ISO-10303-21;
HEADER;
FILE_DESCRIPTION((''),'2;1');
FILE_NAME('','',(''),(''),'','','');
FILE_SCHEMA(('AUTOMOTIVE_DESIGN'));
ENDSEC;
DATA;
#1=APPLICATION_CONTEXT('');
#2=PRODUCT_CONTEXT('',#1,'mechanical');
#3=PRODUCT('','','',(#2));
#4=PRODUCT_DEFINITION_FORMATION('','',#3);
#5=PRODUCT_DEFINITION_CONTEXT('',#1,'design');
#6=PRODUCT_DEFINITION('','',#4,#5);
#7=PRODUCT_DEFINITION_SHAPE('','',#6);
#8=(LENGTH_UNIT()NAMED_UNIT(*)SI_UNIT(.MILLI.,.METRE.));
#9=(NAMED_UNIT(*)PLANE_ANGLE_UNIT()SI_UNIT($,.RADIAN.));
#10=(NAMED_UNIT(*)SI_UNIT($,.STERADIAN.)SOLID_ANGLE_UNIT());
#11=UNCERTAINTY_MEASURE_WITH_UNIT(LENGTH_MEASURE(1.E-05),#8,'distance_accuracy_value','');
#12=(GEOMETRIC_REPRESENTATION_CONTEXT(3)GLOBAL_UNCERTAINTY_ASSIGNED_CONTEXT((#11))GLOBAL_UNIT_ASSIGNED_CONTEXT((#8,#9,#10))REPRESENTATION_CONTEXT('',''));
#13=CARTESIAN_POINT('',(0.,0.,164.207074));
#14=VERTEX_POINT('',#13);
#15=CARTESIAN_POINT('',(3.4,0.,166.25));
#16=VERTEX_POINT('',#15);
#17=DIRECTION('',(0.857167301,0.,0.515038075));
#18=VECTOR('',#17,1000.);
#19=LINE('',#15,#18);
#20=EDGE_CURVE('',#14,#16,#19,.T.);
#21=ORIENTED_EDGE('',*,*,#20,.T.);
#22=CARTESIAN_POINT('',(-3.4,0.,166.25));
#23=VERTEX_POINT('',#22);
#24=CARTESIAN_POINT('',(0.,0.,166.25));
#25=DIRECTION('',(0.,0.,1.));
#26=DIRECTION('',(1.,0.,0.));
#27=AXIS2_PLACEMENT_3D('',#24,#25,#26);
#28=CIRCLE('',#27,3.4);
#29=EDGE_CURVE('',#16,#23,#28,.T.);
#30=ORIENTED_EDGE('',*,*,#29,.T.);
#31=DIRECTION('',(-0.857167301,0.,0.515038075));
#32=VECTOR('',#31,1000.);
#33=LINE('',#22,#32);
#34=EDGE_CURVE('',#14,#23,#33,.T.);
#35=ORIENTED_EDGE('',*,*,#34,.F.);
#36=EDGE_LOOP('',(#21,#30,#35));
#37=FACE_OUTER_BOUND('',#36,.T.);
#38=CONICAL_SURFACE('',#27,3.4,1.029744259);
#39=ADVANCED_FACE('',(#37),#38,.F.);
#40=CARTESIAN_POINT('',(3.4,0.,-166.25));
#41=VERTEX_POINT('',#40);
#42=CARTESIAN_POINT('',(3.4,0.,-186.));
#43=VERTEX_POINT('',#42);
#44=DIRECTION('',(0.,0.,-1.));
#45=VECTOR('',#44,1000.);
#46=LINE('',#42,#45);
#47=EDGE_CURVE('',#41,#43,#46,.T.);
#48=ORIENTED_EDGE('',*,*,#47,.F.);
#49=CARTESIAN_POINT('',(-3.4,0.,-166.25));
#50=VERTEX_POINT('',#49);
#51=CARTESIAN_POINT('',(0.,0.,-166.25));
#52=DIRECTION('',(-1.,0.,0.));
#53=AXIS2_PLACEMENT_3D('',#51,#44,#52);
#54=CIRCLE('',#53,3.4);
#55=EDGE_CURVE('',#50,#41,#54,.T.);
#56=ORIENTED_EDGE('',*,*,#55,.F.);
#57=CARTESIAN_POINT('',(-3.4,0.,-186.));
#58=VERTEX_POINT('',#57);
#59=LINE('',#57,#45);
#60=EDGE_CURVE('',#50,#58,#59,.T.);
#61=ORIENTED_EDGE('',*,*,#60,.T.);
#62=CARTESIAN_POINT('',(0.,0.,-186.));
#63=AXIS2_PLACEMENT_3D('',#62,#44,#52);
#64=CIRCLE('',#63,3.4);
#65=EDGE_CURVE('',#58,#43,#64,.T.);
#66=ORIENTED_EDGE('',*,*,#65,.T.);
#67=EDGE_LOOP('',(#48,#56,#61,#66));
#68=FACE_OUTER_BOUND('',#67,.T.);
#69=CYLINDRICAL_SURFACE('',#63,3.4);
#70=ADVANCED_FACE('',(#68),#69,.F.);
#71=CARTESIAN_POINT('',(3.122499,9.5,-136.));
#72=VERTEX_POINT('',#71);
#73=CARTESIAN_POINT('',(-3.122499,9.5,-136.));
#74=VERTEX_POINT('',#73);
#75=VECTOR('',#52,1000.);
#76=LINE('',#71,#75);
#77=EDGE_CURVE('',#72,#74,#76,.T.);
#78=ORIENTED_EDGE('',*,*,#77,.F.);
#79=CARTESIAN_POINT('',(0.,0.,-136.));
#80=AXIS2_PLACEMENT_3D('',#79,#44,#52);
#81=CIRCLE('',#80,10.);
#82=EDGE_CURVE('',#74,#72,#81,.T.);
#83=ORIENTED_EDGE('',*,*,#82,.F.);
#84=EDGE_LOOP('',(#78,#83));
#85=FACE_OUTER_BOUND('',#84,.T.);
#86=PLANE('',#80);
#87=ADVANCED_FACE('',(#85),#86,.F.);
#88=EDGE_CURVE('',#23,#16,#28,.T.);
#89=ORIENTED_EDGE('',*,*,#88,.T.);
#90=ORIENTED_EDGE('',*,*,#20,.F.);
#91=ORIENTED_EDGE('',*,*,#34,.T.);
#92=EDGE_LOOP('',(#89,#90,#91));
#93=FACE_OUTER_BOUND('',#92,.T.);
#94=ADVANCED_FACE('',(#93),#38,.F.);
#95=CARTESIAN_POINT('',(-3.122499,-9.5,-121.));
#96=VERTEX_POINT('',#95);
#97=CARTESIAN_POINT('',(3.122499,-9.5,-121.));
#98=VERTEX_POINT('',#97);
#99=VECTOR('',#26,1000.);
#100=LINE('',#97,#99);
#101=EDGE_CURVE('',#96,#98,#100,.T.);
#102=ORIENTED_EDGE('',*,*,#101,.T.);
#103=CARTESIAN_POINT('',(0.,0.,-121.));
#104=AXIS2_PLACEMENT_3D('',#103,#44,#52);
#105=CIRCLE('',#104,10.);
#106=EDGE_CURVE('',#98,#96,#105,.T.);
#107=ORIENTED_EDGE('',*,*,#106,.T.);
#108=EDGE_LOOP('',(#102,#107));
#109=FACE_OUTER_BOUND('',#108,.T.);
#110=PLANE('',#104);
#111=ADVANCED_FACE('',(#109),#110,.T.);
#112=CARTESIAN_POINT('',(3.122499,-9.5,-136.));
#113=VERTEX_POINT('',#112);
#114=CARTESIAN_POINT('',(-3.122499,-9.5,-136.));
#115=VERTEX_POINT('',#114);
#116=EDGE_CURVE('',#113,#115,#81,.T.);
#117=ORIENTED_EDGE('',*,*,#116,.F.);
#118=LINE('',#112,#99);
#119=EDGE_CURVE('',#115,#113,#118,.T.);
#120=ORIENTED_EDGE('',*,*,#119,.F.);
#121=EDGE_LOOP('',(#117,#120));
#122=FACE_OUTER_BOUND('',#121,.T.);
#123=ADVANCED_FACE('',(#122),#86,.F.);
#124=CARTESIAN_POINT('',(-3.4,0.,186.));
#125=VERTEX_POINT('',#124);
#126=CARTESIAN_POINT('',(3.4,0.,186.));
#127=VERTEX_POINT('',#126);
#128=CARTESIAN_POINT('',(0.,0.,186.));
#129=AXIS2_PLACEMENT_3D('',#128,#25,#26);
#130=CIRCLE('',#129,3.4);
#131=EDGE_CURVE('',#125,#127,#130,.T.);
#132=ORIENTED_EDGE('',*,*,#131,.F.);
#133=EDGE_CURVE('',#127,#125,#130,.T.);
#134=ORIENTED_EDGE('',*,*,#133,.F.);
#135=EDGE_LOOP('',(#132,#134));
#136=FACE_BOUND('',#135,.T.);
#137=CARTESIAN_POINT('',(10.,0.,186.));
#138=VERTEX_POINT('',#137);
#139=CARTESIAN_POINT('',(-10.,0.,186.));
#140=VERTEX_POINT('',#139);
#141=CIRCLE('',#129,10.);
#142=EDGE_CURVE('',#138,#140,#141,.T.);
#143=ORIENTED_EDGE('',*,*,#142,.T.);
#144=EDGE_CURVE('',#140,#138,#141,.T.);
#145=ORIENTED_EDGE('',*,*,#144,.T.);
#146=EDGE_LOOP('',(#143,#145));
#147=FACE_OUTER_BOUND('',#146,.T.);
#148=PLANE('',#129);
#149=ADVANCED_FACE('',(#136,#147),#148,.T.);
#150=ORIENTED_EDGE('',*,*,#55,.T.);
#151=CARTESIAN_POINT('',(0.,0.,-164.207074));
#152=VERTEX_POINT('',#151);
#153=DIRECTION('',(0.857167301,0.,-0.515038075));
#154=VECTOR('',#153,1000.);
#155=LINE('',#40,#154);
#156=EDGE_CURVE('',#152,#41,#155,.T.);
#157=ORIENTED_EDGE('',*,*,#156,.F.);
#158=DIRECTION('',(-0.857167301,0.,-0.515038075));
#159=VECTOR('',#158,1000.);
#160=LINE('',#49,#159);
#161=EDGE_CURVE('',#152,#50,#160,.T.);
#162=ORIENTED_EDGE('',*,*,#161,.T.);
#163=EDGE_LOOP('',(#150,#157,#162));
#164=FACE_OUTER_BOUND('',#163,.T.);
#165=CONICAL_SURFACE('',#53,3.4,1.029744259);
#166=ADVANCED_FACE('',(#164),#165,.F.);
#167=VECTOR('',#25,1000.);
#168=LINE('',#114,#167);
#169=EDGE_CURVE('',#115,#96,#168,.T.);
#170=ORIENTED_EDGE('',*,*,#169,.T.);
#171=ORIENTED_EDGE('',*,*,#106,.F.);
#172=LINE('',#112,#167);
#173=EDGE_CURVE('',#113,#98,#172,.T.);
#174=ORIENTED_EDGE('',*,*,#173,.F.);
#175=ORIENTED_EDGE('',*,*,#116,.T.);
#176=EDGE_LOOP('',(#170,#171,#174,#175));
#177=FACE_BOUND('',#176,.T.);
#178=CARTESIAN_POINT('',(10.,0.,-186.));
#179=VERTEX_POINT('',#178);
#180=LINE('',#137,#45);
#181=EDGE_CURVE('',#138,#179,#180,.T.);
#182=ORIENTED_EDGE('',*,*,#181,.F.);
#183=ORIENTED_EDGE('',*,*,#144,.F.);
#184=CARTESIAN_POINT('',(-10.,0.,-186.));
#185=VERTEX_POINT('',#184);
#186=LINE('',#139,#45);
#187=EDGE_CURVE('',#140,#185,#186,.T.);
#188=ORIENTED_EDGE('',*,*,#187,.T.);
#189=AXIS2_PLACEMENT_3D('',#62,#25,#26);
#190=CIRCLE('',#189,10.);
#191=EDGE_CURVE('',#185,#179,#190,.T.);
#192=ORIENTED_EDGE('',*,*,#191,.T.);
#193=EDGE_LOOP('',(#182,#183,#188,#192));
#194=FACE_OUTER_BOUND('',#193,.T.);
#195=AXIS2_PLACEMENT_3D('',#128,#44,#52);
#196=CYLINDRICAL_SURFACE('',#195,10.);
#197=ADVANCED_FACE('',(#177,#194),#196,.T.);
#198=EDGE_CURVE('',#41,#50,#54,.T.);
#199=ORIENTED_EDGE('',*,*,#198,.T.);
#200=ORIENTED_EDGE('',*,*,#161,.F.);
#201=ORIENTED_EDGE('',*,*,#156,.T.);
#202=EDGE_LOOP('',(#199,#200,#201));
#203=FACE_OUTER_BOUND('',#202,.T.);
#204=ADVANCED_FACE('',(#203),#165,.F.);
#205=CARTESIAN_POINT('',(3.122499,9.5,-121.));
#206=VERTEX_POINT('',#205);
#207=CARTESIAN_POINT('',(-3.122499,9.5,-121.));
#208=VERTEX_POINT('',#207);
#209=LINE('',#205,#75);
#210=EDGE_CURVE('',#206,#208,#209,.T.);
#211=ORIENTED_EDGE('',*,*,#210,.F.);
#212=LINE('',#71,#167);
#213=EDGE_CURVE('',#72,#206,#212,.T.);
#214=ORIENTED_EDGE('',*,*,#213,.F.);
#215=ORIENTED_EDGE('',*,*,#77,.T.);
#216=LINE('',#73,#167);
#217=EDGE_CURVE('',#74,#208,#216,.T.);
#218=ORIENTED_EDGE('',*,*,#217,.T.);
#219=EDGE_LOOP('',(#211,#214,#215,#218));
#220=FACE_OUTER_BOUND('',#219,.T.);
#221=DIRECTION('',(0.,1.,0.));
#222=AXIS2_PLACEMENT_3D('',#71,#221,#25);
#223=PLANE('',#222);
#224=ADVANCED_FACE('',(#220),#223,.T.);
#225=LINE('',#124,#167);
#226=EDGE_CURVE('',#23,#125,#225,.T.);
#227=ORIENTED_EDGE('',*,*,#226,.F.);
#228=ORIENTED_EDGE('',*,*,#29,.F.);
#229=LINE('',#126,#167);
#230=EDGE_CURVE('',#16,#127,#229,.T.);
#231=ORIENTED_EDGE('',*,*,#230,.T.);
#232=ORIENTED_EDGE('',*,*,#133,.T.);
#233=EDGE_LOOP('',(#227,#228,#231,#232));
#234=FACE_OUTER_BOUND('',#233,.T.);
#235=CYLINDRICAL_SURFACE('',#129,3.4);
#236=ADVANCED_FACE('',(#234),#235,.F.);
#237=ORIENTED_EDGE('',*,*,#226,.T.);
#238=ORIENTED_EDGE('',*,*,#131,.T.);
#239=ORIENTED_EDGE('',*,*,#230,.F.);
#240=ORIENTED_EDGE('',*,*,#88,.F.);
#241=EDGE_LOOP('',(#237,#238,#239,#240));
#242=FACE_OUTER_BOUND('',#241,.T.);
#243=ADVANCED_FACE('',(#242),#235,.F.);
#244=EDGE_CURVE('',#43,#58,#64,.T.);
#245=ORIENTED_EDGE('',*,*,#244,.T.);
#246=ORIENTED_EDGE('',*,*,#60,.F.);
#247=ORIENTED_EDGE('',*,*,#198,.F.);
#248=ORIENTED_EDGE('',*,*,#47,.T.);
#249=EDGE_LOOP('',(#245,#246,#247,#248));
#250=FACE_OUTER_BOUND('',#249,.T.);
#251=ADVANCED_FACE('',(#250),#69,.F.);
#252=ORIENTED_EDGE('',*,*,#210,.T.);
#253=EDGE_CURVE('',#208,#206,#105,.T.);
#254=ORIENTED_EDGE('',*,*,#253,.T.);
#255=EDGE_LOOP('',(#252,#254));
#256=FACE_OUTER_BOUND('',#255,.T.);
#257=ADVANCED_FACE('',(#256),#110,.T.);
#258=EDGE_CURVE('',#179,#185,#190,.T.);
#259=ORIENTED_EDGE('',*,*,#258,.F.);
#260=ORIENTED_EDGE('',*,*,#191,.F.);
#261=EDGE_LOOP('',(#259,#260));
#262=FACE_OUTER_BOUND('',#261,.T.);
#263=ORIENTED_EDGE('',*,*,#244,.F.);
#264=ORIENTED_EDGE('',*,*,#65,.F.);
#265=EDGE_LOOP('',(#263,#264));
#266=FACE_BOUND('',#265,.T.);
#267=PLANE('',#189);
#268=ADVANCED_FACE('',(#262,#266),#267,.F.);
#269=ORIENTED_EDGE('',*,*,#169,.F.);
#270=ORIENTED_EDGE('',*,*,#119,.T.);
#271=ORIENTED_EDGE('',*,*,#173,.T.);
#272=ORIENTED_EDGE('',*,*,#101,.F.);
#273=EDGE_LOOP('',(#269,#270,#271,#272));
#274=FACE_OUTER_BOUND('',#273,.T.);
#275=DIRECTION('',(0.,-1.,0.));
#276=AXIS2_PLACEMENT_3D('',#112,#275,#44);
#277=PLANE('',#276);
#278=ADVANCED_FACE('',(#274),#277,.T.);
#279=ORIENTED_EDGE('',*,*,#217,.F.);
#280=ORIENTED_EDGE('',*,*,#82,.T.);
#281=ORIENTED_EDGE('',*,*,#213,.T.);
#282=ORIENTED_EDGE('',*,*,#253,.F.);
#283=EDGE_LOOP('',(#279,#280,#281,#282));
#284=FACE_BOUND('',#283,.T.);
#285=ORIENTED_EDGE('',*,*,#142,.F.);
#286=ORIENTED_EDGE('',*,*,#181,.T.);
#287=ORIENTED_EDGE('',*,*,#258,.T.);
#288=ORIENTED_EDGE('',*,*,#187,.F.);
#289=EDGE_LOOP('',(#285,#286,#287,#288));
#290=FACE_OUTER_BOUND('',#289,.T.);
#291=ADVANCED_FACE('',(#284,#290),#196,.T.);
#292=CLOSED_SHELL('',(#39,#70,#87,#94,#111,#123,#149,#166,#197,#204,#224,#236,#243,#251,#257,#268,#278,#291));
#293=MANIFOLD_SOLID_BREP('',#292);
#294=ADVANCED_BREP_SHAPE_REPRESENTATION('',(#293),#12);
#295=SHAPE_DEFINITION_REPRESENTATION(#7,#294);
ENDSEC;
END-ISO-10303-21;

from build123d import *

# Parameters (mm, degrees)
SKETCH1_R             = 10
BOSS_EXTRUDE1_DEPTH   = 186
CUT_EXTRUDE1_START    = -65
CUT_EXTRUDE1_DEPTH    = 15
M8_TAPPED_HOLE1_D     = 6.8
M8_TAPPED_HOLE1_DEPTH = 19.75
M8_TAPPED_HOLE1_TIP   = 2.042926105
M8_TAPPED_HOLE2_D     = 6.8
M8_TAPPED_HOLE2_DEPTH = 19.75
M8_TAPPED_HOLE2_TIP   = 2.042926105


with BuildPart() as part:
    # Sketch1 → Boss-Extrude1 (new, symmetric)
    with BuildSketch(Plane.XY):
        with Locations(Location((0, 0, 0), (0, 0, 180))):
            Circle(SKETCH1_R)
    extrude(amount=BOSS_EXTRUDE1_DEPTH, both=True)

    # Sketch2 → Cut-Extrude1 (cut)
    with BuildSketch(Plane(origin=(0, 0, -186), x_dir=(-1, 0, 0), z_dir=(0, 0, -1)).offset(CUT_EXTRUDE1_START)):
        with BuildLine():
            Line((-3.122498999, -9.5), (3.122498999, -9.5))
            ThreePointArc((3.122498999, -9.5), (0, -10), (-3.122498999, -9.5))
        make_face()
        with BuildLine():
            Line((-3.122498999, 9.5), (3.122498999, 9.5))
            ThreePointArc((3.122498999, 9.5), (0, 10), (-3.122498999, 9.5))
        make_face()
    extrude(amount=CUT_EXTRUDE1_DEPTH, mode=Mode.SUBTRACT)

    # M8 Tapped Hole1
    with Locations(Plane(origin=(0, 0, -186), x_dir=(-1, 0, 0), z_dir=(0, 0, -1))):
        with Locations((0, 0)):
            Hole(M8_TAPPED_HOLE1_D / 2, depth=M8_TAPPED_HOLE1_DEPTH)
            with Locations((0, 0, -(M8_TAPPED_HOLE1_DEPTH + M8_TAPPED_HOLE1_TIP / 2))):  # 118° drill point
                Cone(0, M8_TAPPED_HOLE1_D / 2, M8_TAPPED_HOLE1_TIP, mode=Mode.SUBTRACT)

    # M8 Tapped Hole2
    with Locations(Plane.XY.offset(186)):
        with Locations((0, 0)):
            Hole(M8_TAPPED_HOLE2_D / 2, depth=M8_TAPPED_HOLE2_DEPTH)
            with Locations((0, 0, -(M8_TAPPED_HOLE2_DEPTH + M8_TAPPED_HOLE2_TIP / 2))):  # 118° drill point
                Cone(0, M8_TAPPED_HOLE2_D / 2, M8_TAPPED_HOLE2_TIP, mode=Mode.SUBTRACT)


solid = part.part
